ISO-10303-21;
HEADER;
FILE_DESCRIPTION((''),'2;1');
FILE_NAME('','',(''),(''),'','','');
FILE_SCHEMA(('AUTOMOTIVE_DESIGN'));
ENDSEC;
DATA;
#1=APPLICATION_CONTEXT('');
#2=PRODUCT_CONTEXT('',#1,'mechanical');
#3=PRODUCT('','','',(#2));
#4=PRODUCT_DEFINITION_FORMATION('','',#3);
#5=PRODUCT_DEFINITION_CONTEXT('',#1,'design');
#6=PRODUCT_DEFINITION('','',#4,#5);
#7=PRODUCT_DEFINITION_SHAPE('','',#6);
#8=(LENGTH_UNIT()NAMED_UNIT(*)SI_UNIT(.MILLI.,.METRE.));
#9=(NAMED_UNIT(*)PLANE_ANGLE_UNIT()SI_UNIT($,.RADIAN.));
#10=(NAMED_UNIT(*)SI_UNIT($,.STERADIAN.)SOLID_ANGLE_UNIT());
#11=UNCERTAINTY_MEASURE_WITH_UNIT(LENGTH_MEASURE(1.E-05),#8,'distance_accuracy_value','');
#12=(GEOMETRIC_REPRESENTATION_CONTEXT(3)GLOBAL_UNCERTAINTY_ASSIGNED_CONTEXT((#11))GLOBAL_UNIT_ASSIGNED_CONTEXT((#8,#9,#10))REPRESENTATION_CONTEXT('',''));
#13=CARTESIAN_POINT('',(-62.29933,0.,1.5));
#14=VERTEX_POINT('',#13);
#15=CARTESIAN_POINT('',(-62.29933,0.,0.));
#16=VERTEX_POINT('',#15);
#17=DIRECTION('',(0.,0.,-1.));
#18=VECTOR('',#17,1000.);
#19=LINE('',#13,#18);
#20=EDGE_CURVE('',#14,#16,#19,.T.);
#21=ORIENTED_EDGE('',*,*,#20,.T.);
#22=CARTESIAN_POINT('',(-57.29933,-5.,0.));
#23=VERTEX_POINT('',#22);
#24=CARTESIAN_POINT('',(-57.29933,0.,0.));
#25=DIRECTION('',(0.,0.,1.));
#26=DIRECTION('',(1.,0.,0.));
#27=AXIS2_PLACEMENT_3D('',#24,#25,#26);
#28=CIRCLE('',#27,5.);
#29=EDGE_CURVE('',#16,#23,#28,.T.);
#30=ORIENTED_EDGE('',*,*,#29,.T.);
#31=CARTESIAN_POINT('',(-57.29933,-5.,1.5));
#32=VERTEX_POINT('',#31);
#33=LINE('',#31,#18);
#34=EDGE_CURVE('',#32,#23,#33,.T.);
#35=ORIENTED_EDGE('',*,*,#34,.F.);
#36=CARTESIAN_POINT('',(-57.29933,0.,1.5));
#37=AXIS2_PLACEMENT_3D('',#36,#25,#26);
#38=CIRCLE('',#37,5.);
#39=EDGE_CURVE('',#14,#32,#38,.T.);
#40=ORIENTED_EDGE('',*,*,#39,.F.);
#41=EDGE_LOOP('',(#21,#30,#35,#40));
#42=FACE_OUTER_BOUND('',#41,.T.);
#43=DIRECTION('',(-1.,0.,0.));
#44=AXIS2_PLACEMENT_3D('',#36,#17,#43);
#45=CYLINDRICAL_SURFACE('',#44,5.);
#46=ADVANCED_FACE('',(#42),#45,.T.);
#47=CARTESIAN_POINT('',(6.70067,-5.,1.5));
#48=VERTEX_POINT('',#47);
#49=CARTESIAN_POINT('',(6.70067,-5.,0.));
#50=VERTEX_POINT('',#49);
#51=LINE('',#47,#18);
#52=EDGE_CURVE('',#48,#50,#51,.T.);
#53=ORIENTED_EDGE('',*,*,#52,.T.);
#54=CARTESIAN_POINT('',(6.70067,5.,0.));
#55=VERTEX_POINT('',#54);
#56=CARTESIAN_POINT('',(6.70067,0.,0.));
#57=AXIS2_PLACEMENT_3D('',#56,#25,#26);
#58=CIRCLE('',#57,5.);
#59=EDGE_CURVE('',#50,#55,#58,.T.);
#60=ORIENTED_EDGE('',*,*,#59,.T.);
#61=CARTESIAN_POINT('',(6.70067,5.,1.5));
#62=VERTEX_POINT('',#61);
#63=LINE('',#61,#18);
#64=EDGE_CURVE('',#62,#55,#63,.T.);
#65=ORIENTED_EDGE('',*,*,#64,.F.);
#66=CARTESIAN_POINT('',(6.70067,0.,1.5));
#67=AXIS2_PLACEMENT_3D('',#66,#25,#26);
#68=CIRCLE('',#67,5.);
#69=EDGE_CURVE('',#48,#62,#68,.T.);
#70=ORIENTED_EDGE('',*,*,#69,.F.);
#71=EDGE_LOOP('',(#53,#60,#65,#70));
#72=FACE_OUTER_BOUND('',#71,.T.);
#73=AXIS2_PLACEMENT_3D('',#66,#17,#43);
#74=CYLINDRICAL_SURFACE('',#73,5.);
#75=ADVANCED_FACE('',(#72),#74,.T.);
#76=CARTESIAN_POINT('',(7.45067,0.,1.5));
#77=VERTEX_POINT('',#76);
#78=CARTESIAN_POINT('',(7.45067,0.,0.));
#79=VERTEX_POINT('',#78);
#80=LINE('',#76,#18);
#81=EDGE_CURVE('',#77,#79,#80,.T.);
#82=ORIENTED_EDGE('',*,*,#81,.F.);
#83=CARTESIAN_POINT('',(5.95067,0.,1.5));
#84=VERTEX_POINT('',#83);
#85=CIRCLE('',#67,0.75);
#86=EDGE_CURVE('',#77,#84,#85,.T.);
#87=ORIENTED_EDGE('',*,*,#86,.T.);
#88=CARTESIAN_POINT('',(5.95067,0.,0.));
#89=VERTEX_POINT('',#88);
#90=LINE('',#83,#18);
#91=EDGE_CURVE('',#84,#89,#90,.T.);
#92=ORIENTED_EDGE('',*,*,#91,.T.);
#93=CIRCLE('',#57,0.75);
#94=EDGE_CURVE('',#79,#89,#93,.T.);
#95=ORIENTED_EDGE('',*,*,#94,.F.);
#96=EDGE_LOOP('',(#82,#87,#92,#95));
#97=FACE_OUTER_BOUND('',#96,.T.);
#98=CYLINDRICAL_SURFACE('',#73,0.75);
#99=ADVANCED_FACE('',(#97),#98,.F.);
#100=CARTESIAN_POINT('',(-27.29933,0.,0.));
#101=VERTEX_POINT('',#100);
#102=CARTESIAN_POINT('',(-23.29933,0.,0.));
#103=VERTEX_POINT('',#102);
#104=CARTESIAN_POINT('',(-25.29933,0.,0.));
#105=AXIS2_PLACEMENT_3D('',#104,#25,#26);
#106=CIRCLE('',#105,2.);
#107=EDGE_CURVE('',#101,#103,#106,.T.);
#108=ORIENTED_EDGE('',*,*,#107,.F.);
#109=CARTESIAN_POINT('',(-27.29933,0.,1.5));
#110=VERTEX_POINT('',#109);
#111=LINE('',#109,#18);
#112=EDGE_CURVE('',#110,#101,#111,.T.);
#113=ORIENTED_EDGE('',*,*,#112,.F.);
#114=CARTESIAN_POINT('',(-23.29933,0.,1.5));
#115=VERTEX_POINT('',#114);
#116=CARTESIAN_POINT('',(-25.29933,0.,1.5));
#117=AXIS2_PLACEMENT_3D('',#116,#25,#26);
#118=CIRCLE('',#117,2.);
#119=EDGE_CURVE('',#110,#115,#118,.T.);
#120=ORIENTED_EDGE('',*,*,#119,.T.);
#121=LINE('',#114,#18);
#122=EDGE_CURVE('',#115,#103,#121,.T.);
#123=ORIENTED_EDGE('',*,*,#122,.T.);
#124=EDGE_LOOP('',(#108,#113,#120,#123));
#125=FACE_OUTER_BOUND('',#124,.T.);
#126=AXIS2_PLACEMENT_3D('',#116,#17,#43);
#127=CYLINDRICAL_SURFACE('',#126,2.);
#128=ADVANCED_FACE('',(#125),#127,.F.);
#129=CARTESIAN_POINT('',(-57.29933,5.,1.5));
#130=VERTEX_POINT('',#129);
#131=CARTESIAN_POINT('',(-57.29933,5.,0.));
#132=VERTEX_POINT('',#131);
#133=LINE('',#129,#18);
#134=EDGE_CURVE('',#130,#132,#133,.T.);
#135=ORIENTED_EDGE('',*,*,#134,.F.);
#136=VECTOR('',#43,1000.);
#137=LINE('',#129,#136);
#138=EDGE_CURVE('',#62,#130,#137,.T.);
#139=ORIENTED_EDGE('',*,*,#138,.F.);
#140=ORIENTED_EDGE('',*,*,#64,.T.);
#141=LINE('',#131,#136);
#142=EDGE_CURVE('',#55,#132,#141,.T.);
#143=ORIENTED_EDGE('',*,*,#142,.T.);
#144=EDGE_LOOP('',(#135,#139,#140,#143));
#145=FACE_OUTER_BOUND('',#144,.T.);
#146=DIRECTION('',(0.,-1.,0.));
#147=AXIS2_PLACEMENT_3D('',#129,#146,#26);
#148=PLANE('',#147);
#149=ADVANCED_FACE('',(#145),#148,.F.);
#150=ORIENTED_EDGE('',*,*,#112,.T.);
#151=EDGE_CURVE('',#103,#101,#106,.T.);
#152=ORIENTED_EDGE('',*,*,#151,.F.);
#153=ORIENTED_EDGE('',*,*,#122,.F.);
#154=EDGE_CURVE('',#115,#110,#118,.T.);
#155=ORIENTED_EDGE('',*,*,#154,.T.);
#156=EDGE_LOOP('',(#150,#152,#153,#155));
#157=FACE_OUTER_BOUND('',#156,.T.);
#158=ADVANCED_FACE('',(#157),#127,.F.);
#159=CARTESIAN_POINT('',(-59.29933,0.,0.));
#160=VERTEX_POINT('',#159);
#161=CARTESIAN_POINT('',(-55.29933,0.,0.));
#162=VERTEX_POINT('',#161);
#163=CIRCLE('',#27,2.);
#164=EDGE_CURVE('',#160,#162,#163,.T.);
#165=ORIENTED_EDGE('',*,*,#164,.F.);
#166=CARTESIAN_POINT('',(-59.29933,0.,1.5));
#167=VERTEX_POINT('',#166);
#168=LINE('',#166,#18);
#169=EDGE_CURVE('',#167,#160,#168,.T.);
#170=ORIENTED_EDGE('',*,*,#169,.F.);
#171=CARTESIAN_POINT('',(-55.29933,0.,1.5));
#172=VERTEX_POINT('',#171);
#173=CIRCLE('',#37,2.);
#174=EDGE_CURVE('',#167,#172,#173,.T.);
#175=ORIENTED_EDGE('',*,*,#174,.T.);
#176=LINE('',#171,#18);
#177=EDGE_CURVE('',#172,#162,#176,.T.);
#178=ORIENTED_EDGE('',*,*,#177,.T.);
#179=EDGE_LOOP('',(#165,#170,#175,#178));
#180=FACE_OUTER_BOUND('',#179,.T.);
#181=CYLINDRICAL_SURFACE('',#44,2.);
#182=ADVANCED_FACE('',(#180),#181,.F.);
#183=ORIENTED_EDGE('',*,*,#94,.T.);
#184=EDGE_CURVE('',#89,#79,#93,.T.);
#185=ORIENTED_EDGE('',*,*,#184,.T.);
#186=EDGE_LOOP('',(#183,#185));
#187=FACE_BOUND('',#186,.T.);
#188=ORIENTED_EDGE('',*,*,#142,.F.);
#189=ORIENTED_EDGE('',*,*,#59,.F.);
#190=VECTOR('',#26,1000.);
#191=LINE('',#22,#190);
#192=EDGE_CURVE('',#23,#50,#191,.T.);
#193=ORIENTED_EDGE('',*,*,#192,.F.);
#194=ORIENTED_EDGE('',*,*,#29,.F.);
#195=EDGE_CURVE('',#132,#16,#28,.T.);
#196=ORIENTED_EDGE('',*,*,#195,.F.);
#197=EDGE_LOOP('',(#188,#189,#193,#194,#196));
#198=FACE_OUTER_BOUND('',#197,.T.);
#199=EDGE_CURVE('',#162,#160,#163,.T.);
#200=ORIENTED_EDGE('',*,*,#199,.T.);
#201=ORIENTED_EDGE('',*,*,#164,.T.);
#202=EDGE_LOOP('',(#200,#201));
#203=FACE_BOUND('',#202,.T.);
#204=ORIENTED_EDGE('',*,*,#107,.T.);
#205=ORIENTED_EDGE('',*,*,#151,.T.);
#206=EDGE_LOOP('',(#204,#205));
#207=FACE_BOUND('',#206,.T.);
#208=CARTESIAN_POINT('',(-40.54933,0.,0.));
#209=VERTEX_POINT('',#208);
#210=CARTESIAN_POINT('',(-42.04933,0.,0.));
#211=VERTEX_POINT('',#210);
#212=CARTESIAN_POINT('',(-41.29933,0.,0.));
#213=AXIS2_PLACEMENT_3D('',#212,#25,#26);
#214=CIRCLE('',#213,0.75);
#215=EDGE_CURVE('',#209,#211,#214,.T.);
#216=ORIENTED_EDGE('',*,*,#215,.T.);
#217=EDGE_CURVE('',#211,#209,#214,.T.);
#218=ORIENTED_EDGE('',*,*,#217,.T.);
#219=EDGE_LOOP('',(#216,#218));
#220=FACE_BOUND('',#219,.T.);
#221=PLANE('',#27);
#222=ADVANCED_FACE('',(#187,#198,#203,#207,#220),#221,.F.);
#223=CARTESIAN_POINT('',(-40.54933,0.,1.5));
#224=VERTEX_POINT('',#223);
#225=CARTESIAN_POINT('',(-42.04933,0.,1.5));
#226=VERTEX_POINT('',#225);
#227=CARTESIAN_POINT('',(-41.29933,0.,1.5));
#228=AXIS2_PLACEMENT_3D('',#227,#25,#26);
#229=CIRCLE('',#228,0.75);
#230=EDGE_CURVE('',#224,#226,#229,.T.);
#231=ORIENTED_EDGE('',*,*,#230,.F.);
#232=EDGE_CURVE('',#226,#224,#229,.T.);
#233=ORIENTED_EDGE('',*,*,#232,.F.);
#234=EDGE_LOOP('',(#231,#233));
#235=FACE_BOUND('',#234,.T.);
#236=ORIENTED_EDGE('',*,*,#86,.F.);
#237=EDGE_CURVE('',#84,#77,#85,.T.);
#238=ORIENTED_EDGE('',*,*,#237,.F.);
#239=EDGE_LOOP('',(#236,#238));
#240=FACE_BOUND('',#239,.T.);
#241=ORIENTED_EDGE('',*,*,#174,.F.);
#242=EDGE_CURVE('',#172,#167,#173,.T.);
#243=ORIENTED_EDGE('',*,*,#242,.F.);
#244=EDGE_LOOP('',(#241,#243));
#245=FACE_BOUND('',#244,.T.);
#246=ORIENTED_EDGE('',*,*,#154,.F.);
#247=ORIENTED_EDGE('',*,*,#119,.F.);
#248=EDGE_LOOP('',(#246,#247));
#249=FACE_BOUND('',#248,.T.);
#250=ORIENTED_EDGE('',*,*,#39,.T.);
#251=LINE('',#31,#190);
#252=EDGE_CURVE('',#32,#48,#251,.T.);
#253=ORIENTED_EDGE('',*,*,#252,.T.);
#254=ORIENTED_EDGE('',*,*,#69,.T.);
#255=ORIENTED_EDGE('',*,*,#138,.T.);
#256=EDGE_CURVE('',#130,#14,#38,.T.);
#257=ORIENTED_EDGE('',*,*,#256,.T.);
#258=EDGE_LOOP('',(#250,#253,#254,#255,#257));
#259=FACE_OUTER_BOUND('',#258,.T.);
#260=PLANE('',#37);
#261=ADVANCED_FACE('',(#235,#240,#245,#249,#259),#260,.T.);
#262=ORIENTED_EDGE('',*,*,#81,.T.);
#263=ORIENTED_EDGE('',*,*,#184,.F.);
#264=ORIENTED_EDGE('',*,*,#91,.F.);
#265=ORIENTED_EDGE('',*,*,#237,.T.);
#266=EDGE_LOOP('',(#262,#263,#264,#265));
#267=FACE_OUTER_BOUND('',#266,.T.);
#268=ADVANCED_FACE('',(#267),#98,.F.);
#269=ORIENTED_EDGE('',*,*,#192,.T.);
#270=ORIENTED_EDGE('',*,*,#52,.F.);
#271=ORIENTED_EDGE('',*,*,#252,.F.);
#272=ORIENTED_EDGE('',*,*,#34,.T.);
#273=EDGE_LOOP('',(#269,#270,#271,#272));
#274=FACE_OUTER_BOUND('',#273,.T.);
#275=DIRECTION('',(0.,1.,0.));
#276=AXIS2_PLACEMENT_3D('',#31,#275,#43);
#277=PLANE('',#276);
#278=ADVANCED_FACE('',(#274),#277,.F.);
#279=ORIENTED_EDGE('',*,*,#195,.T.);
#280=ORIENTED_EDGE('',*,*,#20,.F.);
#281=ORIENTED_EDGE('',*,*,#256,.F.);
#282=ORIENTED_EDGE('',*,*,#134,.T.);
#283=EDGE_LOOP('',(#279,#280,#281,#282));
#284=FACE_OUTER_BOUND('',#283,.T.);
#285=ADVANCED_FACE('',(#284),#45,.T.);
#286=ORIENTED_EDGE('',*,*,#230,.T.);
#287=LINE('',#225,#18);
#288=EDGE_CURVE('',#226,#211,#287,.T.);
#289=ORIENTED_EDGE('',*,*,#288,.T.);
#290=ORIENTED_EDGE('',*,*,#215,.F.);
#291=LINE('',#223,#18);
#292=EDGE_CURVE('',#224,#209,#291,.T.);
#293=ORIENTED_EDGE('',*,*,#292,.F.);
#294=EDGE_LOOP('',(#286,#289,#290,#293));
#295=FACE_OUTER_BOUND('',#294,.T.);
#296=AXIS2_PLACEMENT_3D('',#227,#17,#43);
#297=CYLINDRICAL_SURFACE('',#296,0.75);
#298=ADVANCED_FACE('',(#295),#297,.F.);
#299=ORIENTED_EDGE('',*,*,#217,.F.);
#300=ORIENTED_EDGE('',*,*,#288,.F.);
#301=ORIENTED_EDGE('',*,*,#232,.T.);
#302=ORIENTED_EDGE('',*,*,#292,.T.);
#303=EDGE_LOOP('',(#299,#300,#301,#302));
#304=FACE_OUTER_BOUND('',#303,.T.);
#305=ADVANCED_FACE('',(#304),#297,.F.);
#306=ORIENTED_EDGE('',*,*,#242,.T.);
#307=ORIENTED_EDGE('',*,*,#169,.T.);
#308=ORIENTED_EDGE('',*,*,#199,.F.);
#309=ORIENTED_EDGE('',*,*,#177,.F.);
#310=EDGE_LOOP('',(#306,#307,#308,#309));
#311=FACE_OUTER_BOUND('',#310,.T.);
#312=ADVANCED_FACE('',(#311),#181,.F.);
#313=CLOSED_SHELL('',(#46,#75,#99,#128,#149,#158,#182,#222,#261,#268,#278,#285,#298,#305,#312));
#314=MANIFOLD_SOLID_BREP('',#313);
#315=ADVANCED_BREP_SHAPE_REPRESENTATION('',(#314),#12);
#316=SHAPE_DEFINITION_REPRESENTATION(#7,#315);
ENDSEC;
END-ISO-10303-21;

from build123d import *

# Parameters (mm, degrees)
SKETCH_1_R           = 2
SKETCH_1_R_2         = 0.75
BOSS_EXTRUDE_1_DEPTH = 1.5


with BuildPart() as part:
    # Sketch 1 → Boss-Extrude 1 (new body)
    with BuildSketch(Plane.XY):
        with BuildLine():
            Line((-57.299329586, 5), (6.700670414, 5))
            ThreePointArc((6.700670414, 5), (11.700670414, 0), (6.700670414, -5))
            Line((6.700670414, -5), (-57.299329586, -5))
            ThreePointArc((-57.299329586, -5), (-62.299329586, 0), (-57.299329586, 5))
        make_face()
        with Locations((-57.299329586, 0)):
            Circle(SKETCH_1_R, mode=Mode.SUBTRACT)
        with Locations((6.700670414, 0)):
            Circle(SKETCH_1_R_2, mode=Mode.SUBTRACT)
        with Locations((-41.299329586, 0)):
            Circle(SKETCH_1_R_2, mode=Mode.SUBTRACT)
        with Locations((-25.299329586, 0)):
            Circle(SKETCH_1_R, mode=Mode.SUBTRACT)
    extrude(amount=BOSS_EXTRUDE_1_DEPTH)


solid = part.part
